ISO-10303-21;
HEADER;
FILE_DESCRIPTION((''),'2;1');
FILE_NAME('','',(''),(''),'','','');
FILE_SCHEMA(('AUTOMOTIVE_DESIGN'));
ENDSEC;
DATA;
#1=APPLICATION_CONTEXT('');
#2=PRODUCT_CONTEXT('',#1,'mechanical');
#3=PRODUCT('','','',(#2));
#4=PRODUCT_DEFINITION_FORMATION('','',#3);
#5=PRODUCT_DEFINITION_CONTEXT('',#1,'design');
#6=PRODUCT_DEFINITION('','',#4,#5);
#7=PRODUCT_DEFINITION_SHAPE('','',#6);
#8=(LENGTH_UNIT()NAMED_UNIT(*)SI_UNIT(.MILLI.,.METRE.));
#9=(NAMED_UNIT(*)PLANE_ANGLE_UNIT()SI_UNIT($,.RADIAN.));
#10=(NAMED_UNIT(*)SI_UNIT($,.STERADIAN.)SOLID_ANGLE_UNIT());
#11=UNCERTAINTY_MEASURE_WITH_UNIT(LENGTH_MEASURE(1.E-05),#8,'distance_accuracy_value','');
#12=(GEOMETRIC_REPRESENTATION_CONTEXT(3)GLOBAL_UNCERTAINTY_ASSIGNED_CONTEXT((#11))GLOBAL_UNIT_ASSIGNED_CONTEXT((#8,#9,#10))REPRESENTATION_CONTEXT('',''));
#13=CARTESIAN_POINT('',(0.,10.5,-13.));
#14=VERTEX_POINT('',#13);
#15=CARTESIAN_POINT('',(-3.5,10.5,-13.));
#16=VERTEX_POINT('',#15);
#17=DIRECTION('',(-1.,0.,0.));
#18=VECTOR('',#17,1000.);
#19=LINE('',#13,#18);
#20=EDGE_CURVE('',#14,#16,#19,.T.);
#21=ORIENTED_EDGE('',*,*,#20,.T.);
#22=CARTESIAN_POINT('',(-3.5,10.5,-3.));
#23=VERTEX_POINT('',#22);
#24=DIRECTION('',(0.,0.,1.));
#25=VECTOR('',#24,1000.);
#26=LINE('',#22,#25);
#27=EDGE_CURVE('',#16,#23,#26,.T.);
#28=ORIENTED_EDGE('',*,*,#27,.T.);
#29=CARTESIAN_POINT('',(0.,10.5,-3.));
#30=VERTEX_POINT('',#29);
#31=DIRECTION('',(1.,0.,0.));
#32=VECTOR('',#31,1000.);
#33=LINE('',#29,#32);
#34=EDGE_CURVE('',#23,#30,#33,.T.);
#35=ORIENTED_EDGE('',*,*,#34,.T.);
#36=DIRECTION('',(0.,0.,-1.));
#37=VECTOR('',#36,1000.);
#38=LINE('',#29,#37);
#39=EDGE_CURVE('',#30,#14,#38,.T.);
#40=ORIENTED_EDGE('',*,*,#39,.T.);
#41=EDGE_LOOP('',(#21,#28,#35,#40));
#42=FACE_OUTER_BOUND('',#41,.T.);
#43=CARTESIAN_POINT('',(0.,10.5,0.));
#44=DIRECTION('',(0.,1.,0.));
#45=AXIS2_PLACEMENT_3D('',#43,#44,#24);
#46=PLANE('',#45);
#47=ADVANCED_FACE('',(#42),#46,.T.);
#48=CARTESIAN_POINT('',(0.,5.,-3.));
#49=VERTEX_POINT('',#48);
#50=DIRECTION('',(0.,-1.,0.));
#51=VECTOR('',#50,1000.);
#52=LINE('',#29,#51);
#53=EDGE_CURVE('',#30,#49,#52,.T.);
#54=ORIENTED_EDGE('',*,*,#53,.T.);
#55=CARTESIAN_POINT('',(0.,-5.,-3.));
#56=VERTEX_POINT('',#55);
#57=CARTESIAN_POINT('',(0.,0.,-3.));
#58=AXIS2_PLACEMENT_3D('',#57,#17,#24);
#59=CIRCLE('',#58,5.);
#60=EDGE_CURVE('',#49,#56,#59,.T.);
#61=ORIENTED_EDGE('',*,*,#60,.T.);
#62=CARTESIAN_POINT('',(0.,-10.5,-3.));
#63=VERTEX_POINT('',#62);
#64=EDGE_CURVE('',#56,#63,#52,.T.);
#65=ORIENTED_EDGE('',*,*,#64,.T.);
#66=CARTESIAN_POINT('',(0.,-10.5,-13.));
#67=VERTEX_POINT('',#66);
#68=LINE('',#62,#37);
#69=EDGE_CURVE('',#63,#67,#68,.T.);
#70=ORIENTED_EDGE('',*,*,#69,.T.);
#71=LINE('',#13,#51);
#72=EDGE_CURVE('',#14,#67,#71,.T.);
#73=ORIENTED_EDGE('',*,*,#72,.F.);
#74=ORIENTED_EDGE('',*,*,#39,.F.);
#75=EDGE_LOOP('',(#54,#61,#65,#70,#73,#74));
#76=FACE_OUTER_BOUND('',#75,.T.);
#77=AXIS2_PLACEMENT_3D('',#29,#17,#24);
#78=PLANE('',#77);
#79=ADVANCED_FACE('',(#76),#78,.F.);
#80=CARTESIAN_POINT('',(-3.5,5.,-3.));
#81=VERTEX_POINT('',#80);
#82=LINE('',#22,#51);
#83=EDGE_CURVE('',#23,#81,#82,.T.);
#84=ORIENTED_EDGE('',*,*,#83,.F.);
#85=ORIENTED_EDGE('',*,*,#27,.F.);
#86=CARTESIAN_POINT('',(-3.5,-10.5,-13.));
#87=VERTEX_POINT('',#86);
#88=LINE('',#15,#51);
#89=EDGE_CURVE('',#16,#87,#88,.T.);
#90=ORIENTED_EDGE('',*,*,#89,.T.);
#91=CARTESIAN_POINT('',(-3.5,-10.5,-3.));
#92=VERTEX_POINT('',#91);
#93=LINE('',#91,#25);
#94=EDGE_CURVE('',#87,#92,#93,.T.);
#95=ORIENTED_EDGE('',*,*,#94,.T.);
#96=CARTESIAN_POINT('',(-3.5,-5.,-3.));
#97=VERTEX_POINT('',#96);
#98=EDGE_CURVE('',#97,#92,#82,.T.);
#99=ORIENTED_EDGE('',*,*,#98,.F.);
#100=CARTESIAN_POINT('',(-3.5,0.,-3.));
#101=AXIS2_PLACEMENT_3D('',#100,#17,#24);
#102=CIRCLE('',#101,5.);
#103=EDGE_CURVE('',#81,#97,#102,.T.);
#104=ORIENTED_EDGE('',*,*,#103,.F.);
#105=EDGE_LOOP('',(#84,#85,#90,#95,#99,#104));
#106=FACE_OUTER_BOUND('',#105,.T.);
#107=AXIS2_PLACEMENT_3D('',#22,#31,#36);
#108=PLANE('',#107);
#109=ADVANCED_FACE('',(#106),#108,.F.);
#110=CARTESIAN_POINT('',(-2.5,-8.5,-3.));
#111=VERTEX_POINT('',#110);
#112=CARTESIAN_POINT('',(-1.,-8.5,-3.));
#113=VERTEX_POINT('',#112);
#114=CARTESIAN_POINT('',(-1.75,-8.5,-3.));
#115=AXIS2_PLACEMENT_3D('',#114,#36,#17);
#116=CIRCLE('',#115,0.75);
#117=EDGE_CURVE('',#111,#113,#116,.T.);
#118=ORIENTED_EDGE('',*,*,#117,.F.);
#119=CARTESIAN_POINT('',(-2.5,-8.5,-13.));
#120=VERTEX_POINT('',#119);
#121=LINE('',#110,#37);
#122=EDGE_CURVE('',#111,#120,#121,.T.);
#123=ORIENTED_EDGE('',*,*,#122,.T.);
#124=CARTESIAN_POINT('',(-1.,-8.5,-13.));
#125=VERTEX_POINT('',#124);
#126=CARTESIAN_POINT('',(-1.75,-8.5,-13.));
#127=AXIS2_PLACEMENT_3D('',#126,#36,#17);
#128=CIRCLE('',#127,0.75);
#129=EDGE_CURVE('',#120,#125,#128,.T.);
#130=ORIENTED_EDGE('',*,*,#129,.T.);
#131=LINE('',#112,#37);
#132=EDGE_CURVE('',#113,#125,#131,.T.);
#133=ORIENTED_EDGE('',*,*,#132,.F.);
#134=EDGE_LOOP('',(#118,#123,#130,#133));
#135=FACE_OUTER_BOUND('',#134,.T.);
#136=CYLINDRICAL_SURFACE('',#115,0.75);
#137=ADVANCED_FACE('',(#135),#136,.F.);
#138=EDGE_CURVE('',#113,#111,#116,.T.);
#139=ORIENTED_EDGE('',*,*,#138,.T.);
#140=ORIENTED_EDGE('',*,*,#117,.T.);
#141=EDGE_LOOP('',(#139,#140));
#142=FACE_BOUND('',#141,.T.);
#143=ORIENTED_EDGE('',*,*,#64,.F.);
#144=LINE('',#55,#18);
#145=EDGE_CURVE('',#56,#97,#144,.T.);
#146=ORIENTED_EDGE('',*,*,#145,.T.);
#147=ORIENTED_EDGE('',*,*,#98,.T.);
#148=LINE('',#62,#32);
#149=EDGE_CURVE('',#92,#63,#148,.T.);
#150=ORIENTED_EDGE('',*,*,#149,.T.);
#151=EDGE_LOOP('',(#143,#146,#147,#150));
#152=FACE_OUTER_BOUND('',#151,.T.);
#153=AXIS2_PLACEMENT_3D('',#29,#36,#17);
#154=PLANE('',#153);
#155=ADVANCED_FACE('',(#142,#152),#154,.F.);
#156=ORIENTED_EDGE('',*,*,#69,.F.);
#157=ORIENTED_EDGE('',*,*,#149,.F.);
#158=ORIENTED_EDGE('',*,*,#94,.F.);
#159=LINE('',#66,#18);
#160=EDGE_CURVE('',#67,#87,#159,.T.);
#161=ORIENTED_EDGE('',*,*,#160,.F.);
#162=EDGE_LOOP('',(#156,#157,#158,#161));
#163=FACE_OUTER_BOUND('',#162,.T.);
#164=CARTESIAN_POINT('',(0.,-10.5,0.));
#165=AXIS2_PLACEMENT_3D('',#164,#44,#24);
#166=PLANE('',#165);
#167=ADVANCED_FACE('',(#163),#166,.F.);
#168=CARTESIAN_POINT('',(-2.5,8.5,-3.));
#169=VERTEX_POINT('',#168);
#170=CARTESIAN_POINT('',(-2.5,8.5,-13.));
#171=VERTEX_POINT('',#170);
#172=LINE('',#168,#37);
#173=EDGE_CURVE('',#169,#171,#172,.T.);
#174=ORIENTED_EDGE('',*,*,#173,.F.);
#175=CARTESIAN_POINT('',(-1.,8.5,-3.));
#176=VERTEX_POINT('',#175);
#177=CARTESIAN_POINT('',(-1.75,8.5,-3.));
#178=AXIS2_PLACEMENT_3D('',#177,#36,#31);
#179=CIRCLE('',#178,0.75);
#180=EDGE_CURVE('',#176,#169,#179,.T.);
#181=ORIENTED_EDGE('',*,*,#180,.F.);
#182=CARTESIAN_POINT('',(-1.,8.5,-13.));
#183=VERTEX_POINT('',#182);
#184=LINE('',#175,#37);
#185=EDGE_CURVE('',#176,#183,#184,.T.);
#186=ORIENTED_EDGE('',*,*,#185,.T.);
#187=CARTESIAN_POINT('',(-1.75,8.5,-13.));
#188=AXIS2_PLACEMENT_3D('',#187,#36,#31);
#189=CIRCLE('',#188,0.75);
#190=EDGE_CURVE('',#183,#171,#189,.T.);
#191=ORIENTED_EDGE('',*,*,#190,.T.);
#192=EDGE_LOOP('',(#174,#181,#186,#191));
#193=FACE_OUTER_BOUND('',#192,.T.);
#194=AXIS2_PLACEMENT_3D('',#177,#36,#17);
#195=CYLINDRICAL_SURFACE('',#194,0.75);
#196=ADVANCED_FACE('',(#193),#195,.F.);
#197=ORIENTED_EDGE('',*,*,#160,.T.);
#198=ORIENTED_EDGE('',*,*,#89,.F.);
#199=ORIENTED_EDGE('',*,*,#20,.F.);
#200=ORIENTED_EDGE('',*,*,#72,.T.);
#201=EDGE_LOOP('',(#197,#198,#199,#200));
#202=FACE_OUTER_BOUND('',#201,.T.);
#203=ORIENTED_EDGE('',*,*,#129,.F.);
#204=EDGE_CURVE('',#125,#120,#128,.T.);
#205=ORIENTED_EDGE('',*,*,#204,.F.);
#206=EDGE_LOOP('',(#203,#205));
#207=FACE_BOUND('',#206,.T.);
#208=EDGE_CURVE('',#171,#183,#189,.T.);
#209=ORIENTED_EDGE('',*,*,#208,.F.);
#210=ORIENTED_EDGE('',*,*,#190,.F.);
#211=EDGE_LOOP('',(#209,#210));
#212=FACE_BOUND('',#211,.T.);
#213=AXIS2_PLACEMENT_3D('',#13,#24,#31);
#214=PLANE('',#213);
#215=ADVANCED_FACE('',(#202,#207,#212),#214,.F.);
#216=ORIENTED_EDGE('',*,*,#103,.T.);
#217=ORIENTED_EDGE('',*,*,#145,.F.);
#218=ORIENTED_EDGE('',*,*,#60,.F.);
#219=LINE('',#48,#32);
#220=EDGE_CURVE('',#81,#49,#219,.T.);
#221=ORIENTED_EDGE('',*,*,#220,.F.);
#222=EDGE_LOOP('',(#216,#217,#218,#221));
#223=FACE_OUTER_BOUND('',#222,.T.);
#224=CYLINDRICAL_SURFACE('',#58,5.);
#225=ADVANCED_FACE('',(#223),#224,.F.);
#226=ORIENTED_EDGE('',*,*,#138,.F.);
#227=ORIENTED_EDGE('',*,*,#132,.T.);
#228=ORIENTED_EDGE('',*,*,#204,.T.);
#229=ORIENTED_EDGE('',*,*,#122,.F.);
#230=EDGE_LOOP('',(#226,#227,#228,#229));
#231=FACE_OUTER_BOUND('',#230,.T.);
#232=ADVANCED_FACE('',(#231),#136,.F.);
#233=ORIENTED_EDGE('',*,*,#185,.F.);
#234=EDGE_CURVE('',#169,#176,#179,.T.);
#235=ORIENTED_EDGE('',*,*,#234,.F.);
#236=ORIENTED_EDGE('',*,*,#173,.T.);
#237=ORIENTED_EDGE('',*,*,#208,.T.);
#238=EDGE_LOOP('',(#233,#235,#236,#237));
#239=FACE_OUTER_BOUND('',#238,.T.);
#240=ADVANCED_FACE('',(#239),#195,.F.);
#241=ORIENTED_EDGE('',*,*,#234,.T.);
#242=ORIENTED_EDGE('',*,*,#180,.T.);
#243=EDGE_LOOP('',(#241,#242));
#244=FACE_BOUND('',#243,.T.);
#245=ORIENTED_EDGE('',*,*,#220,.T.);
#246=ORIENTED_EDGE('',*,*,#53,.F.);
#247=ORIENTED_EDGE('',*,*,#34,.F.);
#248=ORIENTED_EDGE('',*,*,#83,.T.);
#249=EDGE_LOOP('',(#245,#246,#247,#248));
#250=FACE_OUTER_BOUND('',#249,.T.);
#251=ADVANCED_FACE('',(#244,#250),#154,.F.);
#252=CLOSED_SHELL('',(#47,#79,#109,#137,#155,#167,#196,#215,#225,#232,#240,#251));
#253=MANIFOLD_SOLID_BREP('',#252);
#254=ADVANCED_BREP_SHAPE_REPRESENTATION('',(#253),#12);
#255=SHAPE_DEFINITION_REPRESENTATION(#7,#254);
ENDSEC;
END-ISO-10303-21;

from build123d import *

# Parameters (mm, degrees)
SKETCH2_W           = 3.5
SKETCH2_H           = 10
BOSS_EXTRUDE1_DEPTH = 10.5
SKETCH3_R           = 0.75
CUT_EXTRUDE1_DEPTH  = 15.91643389
SKETCH4_R           = 5
CUT_EXTRUDE2_DEPTH  = 18.073371079


with BuildPart() as part:
    # Sketch2 → Boss-Extrude1 (new, symmetric)
    with BuildSketch(Plane(origin=(0, 0, 0), x_dir=(1, 0, 0), z_dir=(0, 1, 0))):
        with Locations((-1.75, 8)):
            Rectangle(SKETCH2_W, SKETCH2_H)
    extrude(amount=BOSS_EXTRUDE1_DEPTH, both=True)

    # Sketch3 → Cut-Extrude1 (cut, through all)
    with BuildSketch(Plane(origin=(0, 0, -13), x_dir=(-1, 0, 0), z_dir=(0, 0, -1))):
        with Locations((1.75, -8.5)):
            Circle(SKETCH3_R)
        with Locations(Location((1.75, 8.5, 0), (0, 0, 180))):
            Circle(SKETCH3_R)
    extrude(amount=-CUT_EXTRUDE1_DEPTH, mode=Mode.SUBTRACT)

    # Sketch4 → Cut-Extrude2 (cut, through all)
    with BuildSketch(Plane.ZY.offset(3.5)):
        with Locations((-3, 0)):
            Circle(SKETCH4_R)
    extrude(amount=-CUT_EXTRUDE2_DEPTH, mode=Mode.SUBTRACT)


solid = part.part
